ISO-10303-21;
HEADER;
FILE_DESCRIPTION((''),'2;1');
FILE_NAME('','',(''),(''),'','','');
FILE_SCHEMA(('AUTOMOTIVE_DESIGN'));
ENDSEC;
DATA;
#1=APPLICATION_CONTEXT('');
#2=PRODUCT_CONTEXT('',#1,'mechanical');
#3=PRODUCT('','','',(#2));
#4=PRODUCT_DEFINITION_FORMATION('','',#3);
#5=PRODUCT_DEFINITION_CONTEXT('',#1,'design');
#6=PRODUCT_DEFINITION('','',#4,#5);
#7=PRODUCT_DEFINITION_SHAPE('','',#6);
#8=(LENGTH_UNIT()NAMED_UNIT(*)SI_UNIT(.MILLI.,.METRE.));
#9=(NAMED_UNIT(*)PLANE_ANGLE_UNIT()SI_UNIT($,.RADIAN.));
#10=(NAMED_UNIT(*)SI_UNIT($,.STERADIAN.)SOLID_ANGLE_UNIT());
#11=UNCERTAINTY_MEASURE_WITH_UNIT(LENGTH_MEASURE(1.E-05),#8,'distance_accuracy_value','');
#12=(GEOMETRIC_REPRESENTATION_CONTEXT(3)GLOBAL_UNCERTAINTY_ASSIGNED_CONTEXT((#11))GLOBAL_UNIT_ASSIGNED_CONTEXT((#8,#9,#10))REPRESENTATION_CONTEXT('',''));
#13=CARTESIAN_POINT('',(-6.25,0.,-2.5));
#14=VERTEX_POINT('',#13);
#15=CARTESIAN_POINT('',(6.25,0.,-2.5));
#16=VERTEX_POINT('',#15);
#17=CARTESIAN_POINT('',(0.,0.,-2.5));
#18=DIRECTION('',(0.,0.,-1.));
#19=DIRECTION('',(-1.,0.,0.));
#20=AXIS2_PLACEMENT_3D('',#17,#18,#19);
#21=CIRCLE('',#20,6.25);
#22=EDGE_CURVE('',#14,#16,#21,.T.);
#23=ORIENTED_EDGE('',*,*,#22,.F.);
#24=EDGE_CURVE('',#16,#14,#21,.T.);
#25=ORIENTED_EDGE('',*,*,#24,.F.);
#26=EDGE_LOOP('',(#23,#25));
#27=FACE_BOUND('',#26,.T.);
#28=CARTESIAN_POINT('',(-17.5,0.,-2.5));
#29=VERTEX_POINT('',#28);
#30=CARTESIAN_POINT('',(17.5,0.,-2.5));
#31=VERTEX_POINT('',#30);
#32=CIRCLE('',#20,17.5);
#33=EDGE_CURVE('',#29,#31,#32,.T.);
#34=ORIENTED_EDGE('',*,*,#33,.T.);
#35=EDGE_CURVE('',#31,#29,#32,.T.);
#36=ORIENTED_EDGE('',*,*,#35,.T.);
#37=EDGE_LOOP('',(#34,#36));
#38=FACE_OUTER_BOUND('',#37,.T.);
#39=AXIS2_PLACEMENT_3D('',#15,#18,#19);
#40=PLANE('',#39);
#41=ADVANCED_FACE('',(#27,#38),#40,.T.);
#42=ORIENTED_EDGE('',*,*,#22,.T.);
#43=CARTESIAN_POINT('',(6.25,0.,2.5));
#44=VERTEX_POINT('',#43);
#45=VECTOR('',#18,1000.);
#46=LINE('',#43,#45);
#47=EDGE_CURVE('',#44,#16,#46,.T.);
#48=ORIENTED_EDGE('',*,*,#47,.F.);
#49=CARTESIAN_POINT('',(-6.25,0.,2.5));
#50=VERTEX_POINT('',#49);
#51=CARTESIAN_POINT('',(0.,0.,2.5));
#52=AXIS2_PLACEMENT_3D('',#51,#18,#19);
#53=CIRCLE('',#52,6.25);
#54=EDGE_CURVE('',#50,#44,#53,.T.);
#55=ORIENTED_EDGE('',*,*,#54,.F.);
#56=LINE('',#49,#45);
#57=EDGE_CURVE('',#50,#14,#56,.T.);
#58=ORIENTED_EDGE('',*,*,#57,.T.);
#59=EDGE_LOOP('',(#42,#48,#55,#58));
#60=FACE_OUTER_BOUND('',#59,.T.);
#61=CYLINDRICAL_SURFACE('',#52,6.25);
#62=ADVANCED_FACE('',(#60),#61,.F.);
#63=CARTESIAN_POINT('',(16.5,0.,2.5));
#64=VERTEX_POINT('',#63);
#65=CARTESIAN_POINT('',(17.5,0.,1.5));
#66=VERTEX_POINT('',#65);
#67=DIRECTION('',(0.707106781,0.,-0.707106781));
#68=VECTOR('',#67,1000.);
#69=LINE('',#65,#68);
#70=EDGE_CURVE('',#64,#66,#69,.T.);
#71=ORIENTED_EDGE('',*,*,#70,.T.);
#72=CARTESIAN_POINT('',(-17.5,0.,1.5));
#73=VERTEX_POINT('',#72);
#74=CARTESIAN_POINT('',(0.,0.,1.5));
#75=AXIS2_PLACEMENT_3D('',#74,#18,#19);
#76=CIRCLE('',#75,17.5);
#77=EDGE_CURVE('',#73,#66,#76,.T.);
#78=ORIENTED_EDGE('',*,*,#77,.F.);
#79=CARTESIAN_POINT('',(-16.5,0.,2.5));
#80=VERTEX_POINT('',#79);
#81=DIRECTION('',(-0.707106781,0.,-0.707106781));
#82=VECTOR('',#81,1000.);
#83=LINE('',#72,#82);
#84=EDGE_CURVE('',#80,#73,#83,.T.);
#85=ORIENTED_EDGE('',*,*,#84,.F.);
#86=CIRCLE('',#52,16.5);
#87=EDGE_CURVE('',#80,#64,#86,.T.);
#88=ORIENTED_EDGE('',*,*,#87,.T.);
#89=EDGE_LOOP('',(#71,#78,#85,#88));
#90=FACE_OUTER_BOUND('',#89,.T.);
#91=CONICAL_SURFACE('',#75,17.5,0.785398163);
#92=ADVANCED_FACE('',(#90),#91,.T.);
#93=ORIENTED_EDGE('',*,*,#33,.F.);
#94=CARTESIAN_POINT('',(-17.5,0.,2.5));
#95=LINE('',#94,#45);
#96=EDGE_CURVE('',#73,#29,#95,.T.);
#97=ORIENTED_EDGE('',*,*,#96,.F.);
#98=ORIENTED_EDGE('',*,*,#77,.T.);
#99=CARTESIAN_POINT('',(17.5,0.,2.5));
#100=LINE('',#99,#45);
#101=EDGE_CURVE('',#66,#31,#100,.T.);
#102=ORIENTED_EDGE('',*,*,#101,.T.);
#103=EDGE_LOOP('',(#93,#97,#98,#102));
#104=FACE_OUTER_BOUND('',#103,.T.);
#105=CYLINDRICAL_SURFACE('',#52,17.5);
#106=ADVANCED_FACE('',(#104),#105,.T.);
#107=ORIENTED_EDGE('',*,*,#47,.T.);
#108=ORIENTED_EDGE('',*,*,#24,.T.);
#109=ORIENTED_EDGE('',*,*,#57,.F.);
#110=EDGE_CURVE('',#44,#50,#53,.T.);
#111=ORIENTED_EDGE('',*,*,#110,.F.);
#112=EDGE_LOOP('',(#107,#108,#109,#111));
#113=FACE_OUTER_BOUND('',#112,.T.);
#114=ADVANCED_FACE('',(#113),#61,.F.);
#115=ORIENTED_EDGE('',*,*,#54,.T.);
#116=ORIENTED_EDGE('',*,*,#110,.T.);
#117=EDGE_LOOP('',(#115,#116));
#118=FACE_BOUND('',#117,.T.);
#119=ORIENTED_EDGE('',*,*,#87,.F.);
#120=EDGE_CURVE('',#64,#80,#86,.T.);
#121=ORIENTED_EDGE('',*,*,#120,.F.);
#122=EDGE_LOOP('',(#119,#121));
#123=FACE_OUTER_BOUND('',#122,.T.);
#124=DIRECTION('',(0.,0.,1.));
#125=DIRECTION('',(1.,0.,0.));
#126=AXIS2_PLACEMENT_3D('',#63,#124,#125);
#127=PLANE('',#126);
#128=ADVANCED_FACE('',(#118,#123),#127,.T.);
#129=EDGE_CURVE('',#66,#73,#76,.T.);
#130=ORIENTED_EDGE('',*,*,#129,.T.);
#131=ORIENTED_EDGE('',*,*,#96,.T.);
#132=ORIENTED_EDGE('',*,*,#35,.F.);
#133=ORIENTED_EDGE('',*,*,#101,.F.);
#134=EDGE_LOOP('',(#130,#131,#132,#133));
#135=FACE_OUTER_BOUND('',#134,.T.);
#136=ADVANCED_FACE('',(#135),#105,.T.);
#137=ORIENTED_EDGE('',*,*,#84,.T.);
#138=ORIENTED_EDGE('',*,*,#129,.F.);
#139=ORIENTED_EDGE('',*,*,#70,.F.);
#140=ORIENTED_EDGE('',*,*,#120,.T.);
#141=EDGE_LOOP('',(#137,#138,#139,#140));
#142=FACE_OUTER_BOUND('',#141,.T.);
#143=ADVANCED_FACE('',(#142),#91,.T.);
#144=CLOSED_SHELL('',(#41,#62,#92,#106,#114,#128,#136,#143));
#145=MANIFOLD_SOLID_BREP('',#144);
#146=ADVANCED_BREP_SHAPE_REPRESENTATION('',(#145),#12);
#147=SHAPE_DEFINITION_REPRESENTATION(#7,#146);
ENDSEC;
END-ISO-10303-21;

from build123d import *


with BuildPart() as part:
    # 草图1 → 旋转1 (revolve)
    with BuildSketch(Plane.XZ, mode=Mode.PRIVATE) as revolve_1_sk:
        Polygon((6.25, 2.5), (6.25, -2.5), (17.5, -2.5), (17.5, 1.5), (16.5, 2.5), align=None)
    revolve(revolve_1_sk.sketch.rotate(Axis((0, 0, 2.5), (0, 0, -1)), 180), axis=Axis((0, 0, 2.5), (0, 0, -1)))


solid = part.part
